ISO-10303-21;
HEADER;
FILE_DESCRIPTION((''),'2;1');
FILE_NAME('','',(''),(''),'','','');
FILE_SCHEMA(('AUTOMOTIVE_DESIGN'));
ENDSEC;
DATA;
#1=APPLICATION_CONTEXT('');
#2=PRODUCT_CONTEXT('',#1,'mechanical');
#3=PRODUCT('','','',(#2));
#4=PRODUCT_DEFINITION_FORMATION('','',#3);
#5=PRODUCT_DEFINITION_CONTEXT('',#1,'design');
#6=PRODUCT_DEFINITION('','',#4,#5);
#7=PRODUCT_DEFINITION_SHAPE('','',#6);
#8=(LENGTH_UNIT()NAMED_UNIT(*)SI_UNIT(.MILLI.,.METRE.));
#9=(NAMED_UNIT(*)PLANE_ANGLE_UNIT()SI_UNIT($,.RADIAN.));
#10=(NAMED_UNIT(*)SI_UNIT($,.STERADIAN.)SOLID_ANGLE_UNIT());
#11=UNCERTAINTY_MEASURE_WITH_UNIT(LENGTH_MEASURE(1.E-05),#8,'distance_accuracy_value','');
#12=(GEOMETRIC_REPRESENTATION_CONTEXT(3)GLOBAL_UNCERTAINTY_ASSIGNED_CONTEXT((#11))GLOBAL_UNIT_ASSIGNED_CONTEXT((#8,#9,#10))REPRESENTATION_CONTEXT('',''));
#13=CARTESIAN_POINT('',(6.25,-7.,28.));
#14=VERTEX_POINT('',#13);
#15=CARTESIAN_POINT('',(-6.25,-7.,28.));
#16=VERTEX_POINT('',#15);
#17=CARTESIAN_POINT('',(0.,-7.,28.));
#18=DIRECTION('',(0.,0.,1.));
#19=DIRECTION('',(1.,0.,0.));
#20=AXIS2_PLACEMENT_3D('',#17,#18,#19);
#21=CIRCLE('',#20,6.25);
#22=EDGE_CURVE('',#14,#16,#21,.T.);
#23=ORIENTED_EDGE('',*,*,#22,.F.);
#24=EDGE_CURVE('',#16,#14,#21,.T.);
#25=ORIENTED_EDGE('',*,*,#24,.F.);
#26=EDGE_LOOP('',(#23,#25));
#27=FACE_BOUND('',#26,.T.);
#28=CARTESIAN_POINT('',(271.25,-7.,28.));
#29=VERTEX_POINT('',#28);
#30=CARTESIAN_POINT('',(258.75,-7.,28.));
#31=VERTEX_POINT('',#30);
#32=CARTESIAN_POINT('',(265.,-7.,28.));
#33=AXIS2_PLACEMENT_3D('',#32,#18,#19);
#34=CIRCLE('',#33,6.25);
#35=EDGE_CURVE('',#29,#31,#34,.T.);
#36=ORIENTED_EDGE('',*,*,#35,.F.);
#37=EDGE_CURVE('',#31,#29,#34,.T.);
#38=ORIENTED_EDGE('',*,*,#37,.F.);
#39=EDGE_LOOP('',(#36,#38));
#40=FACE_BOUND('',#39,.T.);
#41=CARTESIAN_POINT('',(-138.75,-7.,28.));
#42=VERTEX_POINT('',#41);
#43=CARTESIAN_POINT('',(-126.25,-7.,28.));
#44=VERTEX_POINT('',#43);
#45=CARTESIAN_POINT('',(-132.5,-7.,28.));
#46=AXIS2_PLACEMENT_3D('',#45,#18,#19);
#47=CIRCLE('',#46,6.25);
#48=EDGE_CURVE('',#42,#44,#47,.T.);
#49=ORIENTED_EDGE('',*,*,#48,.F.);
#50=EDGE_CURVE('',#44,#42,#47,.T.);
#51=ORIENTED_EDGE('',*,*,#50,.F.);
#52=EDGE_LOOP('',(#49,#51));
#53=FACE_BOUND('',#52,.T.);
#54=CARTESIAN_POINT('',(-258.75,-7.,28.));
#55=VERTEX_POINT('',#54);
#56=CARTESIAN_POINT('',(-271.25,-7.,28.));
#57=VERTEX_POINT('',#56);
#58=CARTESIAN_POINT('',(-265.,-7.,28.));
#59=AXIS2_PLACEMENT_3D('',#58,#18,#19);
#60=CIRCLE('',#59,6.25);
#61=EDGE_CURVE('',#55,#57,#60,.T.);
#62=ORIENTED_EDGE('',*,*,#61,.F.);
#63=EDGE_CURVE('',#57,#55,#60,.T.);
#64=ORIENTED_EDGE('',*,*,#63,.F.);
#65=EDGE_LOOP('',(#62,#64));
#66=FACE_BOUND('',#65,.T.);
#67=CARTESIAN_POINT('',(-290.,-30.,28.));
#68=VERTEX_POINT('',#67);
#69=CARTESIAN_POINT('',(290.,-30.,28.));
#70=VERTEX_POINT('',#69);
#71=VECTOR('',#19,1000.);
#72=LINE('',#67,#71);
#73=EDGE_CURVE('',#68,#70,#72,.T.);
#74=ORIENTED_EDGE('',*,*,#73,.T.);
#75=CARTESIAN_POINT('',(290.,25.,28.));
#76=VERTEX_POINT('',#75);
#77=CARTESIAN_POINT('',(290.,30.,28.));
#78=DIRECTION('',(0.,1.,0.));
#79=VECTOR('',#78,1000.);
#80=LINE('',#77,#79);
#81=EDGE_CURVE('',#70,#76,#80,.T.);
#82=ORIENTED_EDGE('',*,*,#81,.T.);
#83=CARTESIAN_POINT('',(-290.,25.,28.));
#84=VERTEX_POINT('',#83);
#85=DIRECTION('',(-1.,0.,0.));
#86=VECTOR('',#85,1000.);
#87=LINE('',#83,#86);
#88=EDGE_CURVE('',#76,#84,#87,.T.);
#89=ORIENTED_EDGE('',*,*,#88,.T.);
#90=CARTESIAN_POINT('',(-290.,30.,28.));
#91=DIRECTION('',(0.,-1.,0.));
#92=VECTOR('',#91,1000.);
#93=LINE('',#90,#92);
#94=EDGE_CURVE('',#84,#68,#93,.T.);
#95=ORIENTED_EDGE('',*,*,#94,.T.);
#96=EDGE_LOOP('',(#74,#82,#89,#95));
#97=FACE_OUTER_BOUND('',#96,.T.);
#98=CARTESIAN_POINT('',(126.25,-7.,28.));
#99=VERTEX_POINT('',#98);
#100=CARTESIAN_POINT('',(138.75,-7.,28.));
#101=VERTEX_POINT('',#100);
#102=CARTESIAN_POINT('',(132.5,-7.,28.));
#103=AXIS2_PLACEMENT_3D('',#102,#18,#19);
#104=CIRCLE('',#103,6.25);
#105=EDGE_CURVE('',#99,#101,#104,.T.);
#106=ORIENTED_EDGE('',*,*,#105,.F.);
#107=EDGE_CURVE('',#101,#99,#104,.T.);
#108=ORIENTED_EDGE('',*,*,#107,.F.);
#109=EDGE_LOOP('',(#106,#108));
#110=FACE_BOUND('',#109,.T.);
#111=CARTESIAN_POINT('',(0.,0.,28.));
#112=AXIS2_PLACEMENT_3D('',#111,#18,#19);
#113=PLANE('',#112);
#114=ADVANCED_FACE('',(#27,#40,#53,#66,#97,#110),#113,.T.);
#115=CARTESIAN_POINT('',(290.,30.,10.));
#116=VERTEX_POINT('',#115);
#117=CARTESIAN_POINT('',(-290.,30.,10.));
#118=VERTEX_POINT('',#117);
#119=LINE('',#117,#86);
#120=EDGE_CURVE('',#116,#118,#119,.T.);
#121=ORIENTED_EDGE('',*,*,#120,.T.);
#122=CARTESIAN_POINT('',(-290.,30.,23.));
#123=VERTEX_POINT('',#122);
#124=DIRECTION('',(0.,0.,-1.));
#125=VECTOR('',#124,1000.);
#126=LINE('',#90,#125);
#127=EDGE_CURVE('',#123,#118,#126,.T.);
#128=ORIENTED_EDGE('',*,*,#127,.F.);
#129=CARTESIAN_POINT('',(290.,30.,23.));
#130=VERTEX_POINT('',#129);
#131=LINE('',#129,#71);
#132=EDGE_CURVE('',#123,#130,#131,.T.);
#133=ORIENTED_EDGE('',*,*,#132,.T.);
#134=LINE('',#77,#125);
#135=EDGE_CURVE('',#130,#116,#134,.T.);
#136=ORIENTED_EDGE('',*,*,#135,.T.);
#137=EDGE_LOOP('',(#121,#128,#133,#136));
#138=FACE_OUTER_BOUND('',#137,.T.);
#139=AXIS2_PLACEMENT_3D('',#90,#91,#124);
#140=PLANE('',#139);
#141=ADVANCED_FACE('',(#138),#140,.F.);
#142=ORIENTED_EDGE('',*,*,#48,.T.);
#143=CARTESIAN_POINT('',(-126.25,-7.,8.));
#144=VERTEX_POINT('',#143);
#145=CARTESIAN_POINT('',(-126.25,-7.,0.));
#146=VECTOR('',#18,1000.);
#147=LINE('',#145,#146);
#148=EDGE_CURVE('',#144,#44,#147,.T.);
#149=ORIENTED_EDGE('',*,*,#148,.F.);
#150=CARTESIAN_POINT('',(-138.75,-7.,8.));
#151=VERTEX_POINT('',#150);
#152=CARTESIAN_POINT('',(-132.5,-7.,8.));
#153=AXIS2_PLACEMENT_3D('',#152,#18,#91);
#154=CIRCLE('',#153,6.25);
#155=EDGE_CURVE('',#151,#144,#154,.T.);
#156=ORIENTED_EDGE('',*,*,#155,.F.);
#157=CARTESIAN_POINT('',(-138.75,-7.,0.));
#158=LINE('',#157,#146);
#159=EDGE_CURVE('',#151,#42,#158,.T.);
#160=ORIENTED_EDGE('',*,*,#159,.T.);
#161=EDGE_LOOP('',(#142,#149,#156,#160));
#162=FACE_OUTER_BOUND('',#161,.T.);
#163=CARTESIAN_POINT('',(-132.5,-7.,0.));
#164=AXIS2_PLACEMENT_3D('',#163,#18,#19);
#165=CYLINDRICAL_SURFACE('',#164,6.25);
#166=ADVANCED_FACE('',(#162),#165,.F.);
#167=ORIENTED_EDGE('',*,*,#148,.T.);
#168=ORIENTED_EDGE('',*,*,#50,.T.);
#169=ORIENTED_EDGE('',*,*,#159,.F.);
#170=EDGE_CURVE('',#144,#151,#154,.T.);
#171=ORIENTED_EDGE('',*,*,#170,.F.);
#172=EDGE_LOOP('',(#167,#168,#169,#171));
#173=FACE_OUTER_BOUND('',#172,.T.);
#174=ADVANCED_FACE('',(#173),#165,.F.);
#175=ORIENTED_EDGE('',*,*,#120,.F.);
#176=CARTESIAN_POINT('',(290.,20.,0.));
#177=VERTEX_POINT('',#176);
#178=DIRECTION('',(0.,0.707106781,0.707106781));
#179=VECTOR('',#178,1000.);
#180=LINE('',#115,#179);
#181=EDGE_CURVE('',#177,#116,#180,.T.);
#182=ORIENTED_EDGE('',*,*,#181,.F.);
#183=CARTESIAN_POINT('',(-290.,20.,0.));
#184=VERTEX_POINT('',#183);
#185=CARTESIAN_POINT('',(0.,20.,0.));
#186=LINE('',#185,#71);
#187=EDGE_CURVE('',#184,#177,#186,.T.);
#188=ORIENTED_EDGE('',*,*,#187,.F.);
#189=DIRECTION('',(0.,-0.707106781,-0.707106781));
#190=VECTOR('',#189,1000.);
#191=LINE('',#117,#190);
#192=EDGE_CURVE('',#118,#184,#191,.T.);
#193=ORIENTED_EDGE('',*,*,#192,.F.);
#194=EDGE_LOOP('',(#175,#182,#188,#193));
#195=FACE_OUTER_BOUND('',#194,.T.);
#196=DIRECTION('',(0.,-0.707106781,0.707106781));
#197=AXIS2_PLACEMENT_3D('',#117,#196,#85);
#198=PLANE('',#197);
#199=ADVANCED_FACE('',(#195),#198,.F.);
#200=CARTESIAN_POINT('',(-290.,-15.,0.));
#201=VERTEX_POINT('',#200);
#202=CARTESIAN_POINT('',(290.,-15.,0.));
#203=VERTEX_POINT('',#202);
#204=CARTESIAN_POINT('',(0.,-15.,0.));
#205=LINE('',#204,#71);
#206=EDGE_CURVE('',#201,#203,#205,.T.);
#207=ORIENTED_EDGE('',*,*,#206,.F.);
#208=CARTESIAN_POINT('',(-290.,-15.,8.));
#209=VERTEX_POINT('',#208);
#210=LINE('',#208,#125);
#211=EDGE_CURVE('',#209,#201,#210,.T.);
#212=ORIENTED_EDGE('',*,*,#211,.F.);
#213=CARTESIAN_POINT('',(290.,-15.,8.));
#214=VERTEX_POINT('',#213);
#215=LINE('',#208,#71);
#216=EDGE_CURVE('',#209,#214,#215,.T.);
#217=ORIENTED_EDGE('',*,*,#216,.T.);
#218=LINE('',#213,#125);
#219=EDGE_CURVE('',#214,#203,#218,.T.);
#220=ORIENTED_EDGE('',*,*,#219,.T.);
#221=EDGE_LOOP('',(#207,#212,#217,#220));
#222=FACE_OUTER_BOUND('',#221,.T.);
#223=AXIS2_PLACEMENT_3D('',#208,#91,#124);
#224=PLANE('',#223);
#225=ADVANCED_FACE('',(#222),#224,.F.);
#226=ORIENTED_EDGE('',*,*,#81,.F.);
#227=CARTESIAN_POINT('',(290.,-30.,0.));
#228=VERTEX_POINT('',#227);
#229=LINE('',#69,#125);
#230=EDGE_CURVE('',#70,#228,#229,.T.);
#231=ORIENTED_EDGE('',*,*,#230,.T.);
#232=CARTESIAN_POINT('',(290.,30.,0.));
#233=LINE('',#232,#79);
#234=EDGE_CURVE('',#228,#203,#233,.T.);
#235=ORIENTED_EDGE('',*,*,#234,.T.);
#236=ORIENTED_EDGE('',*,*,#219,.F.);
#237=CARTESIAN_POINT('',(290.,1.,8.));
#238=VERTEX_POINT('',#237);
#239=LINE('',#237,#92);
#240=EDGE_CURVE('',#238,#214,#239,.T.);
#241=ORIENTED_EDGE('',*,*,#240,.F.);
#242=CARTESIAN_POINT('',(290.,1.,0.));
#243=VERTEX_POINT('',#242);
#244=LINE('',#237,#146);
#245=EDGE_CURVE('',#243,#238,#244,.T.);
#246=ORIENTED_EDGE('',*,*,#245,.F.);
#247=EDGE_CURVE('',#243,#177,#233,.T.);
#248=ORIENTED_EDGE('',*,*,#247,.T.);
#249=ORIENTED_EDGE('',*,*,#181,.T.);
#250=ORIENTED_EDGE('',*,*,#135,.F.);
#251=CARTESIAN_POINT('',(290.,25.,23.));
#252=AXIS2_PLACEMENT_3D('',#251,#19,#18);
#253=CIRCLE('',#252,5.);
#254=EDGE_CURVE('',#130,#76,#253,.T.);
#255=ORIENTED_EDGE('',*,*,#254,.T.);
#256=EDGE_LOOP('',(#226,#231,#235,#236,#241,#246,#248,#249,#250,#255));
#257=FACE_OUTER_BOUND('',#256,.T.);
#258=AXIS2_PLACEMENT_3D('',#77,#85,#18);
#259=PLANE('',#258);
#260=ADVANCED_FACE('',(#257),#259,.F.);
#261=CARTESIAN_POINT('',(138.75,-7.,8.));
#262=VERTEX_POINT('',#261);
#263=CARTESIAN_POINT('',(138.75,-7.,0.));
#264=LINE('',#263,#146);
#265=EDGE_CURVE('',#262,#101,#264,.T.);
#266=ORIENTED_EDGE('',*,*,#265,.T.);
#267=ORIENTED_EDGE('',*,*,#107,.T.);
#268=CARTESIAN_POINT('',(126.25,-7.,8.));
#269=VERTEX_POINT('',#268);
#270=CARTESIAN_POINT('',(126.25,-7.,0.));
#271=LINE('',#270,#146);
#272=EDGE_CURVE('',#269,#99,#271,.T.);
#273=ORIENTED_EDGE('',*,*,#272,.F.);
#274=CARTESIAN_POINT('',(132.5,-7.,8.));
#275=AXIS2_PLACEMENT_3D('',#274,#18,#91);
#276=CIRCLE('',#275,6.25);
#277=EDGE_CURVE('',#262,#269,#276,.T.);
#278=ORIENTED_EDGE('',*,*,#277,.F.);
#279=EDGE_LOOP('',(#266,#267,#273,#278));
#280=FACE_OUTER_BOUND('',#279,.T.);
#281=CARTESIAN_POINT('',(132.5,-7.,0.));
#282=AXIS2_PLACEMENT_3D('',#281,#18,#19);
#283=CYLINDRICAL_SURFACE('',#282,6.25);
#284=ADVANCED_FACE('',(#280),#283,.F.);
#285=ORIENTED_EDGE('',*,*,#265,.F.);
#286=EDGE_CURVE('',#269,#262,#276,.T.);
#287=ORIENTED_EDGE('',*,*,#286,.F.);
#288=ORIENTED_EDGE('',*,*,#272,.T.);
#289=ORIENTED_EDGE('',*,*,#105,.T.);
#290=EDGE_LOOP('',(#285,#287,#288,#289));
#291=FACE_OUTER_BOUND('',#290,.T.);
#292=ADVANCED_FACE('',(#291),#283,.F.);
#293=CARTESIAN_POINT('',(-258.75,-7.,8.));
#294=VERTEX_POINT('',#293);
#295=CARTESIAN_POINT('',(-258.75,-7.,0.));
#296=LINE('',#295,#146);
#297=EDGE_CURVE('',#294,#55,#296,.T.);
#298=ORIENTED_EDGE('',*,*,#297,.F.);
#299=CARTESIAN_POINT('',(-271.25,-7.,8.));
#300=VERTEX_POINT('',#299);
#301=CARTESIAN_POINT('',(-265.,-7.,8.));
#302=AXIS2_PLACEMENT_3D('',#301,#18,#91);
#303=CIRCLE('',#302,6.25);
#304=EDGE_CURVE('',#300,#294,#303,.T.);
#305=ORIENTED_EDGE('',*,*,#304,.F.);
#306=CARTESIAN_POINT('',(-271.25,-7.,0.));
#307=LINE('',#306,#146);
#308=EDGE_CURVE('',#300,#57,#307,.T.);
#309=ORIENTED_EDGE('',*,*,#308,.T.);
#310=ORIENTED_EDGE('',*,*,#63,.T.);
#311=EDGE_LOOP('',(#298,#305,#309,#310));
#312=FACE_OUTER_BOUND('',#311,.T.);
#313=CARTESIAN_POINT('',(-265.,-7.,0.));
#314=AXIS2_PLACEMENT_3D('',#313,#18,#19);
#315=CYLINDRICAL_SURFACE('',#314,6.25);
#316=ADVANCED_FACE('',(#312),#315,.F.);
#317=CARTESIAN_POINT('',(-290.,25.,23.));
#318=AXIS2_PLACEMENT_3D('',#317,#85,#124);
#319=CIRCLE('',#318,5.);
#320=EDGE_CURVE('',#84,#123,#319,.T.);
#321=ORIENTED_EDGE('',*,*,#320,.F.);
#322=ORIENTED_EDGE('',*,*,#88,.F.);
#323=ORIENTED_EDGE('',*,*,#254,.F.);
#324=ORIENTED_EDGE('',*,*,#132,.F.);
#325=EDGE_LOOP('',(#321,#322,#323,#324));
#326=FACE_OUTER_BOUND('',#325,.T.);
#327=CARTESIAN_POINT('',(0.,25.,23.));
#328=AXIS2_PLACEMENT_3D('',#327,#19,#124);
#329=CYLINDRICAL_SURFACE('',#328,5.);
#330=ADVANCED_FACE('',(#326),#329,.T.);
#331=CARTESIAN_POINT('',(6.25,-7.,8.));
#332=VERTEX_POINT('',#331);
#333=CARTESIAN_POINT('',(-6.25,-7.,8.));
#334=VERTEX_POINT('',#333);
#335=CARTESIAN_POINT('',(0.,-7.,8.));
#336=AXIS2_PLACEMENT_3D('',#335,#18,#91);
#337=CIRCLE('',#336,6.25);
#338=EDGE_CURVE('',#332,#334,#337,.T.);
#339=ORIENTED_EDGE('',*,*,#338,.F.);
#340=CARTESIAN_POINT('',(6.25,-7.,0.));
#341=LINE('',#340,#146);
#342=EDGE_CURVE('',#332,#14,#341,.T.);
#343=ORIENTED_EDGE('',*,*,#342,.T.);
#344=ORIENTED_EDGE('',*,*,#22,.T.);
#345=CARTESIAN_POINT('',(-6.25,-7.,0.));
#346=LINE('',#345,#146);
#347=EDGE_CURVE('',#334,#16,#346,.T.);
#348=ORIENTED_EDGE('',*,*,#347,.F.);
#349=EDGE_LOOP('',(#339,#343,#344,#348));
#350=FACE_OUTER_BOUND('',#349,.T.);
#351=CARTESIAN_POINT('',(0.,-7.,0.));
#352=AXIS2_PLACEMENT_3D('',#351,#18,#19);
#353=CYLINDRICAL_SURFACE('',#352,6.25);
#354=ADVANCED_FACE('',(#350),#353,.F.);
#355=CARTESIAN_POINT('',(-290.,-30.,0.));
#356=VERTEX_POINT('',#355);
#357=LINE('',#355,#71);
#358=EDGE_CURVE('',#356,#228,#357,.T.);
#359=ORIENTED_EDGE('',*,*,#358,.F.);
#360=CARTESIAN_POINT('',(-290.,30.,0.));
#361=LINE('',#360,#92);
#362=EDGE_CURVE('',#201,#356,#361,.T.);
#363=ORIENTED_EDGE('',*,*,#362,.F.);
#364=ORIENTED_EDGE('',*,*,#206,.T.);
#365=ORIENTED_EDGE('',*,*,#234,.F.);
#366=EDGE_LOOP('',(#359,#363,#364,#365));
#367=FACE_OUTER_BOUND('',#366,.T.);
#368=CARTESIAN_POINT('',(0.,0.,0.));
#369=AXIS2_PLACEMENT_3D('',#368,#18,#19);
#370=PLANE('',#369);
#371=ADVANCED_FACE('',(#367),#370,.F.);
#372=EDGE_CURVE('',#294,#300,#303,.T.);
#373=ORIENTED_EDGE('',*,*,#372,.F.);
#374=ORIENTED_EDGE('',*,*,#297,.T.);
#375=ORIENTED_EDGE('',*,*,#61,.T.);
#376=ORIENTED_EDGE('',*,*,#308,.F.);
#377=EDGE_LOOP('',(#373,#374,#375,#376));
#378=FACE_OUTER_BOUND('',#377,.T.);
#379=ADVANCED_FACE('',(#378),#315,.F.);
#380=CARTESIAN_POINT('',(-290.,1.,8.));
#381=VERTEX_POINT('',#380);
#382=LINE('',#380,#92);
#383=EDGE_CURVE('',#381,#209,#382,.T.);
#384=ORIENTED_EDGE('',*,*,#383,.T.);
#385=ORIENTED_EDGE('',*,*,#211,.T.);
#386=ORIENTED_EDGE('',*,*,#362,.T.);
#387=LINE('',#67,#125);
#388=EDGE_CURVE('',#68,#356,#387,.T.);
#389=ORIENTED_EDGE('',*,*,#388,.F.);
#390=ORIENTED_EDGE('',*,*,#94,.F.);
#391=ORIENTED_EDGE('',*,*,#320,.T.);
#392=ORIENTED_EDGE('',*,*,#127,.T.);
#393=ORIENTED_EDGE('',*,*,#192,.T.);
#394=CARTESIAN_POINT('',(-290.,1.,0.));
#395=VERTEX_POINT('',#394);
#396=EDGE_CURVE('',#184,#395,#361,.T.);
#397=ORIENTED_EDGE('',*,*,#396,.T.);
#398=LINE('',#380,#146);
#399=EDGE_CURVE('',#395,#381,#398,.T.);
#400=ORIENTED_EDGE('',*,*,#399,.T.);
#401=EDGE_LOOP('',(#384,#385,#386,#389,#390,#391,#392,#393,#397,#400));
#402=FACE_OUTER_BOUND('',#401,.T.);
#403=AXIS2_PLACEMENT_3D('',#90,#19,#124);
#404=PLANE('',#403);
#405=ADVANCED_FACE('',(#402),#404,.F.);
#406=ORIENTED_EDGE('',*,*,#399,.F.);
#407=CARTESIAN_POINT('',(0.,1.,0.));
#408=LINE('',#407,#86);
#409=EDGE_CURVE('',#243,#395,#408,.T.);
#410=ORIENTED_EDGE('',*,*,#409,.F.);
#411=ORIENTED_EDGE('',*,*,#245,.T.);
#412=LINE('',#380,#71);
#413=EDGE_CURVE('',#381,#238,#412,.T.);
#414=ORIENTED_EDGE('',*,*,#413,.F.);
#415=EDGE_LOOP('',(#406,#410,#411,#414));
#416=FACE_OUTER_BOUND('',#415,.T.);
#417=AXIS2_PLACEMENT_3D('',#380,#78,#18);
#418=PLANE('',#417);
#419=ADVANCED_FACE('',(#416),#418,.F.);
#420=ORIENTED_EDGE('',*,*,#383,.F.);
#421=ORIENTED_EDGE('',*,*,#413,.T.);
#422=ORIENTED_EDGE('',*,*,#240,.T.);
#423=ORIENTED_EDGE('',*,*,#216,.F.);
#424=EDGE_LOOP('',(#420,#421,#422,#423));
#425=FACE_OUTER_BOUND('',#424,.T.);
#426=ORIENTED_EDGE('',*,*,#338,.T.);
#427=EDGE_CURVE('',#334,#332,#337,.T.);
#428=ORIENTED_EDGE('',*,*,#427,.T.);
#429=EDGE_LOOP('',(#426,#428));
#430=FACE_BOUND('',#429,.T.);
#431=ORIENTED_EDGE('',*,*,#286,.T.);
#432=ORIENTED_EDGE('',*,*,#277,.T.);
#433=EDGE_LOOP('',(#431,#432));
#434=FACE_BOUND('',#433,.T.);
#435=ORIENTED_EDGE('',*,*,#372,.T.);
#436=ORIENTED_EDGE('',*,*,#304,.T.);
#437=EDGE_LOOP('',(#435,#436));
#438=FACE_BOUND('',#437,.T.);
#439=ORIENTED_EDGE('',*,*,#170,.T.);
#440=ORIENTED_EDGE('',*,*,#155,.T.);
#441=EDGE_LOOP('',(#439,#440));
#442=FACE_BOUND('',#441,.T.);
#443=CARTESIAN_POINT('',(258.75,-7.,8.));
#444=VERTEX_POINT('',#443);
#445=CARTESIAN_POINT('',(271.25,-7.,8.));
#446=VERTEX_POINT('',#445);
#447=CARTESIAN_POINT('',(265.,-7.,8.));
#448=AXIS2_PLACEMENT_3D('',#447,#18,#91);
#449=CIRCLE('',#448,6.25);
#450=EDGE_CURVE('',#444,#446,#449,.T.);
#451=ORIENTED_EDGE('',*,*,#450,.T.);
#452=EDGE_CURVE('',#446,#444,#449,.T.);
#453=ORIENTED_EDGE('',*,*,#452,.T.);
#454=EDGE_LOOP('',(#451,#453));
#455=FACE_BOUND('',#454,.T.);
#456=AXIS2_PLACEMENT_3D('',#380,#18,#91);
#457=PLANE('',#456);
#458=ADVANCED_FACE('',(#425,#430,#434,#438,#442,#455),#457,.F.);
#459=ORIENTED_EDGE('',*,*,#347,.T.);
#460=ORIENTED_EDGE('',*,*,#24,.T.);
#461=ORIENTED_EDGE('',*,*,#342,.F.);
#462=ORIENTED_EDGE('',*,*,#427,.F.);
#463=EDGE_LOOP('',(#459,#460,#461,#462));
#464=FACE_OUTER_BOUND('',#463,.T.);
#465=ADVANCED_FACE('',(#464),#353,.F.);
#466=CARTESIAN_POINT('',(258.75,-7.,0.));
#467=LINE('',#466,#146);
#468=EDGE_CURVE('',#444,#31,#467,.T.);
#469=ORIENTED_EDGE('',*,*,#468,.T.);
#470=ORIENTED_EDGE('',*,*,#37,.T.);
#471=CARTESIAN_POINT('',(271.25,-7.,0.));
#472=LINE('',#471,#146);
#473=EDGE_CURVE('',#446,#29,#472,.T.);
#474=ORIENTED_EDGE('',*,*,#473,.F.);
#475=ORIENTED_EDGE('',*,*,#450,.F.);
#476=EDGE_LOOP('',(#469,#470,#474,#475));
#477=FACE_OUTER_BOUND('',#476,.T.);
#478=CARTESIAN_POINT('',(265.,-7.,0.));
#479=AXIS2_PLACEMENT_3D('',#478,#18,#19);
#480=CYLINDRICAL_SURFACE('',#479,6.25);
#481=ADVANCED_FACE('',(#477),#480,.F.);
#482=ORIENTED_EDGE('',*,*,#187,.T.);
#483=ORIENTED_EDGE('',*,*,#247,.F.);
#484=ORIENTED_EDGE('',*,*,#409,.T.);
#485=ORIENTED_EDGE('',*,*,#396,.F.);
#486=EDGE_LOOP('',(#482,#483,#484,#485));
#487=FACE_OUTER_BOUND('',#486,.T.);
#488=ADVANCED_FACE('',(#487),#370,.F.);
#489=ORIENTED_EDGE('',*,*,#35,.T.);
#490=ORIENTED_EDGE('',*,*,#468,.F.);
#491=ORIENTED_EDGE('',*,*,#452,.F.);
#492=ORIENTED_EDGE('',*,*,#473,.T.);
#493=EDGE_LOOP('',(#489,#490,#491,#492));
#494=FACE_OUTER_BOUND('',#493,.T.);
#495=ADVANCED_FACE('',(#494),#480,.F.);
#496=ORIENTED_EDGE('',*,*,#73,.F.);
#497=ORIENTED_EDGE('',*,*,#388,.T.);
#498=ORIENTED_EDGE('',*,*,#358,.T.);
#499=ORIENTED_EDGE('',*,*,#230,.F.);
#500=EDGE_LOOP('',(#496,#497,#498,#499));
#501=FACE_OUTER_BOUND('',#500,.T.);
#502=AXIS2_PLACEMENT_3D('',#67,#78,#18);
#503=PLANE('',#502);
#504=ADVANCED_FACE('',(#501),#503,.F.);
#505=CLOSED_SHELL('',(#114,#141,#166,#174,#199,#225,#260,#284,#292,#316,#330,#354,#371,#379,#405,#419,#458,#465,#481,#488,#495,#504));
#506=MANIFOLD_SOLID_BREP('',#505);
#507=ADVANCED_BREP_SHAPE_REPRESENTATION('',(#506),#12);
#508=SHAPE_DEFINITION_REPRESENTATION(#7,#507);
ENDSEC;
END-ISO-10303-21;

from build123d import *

# Parameters (mm, degrees)
RAIL_PROFILE_SKETCH_W           = 580
RAIL_PROFILE_SKETCH_H           = 60
RAIL_BAR_580X60X28_DEPTH        = 28
EDGE_FILLET_R5_R                = 5
GROOVE_SKETCH_W                 = 16
GROOVE_SKETCH_H                 = 16
LONGITUDINAL_GROOVE_16X16_DEPTH = 582.449911858
EDGE_CHAMFER_10X45_SIZE         = 10
MOUNTING_HOLES_SKETCH_R         = 6.25
MOUNTING_HOLES_5X_DEPTH         = 293.889057494


with BuildPart() as part:
    # Rail Profile Sketch → Rail Bar 580x60x28 (new body)
    with BuildSketch(Plane.XY):
        Rectangle(RAIL_PROFILE_SKETCH_W, RAIL_PROFILE_SKETCH_H)
    extrude(amount=RAIL_BAR_580X60X28_DEPTH)

    # Edge Fillet R5
    edge_fillet_r5_edges = [part.edges().sort_by_distance(p)[0] for p in [
        (0, 30, 28),
    ]]
    fillet(edge_fillet_r5_edges, radius=EDGE_FILLET_R5_R)

    # Groove Sketch → Longitudinal Groove 16x16 (cut, through all)
    with BuildSketch(Plane(origin=(290, 0, 0), x_dir=(0, 0, -1), z_dir=(1, 0, 0))):
        with Locations((0, -7)):
            Rectangle(GROOVE_SKETCH_W, GROOVE_SKETCH_H)
    extrude(amount=-LONGITUDINAL_GROOVE_16X16_DEPTH, mode=Mode.SUBTRACT)

    # Edge Chamfer 10x45
    edge_chamfer_10x45_edges = [part.edges().sort_by_distance(p)[0] for p in [
        (0, 30, 0),
    ]]
    chamfer(edge_chamfer_10x45_edges, length=EDGE_CHAMFER_10X45_SIZE)

    # Mounting Holes Sketch → Mounting Holes 5x (cut, through all)
    with BuildSketch(Plane.XY.offset(28)):
        with Locations((-265, -7)):
            Circle(MOUNTING_HOLES_SKETCH_R)
        with Locations((-132.5, -7)):
            Circle(MOUNTING_HOLES_SKETCH_R)
        with Locations((0, -7)):
            Circle(MOUNTING_HOLES_SKETCH_R)
        with Locations((132.5, -7)):
            Circle(MOUNTING_HOLES_SKETCH_R)
        with Locations((265, -7)):
            Circle(MOUNTING_HOLES_SKETCH_R)
    extrude(amount=-MOUNTING_HOLES_5X_DEPTH, mode=Mode.SUBTRACT)


solid = part.part
